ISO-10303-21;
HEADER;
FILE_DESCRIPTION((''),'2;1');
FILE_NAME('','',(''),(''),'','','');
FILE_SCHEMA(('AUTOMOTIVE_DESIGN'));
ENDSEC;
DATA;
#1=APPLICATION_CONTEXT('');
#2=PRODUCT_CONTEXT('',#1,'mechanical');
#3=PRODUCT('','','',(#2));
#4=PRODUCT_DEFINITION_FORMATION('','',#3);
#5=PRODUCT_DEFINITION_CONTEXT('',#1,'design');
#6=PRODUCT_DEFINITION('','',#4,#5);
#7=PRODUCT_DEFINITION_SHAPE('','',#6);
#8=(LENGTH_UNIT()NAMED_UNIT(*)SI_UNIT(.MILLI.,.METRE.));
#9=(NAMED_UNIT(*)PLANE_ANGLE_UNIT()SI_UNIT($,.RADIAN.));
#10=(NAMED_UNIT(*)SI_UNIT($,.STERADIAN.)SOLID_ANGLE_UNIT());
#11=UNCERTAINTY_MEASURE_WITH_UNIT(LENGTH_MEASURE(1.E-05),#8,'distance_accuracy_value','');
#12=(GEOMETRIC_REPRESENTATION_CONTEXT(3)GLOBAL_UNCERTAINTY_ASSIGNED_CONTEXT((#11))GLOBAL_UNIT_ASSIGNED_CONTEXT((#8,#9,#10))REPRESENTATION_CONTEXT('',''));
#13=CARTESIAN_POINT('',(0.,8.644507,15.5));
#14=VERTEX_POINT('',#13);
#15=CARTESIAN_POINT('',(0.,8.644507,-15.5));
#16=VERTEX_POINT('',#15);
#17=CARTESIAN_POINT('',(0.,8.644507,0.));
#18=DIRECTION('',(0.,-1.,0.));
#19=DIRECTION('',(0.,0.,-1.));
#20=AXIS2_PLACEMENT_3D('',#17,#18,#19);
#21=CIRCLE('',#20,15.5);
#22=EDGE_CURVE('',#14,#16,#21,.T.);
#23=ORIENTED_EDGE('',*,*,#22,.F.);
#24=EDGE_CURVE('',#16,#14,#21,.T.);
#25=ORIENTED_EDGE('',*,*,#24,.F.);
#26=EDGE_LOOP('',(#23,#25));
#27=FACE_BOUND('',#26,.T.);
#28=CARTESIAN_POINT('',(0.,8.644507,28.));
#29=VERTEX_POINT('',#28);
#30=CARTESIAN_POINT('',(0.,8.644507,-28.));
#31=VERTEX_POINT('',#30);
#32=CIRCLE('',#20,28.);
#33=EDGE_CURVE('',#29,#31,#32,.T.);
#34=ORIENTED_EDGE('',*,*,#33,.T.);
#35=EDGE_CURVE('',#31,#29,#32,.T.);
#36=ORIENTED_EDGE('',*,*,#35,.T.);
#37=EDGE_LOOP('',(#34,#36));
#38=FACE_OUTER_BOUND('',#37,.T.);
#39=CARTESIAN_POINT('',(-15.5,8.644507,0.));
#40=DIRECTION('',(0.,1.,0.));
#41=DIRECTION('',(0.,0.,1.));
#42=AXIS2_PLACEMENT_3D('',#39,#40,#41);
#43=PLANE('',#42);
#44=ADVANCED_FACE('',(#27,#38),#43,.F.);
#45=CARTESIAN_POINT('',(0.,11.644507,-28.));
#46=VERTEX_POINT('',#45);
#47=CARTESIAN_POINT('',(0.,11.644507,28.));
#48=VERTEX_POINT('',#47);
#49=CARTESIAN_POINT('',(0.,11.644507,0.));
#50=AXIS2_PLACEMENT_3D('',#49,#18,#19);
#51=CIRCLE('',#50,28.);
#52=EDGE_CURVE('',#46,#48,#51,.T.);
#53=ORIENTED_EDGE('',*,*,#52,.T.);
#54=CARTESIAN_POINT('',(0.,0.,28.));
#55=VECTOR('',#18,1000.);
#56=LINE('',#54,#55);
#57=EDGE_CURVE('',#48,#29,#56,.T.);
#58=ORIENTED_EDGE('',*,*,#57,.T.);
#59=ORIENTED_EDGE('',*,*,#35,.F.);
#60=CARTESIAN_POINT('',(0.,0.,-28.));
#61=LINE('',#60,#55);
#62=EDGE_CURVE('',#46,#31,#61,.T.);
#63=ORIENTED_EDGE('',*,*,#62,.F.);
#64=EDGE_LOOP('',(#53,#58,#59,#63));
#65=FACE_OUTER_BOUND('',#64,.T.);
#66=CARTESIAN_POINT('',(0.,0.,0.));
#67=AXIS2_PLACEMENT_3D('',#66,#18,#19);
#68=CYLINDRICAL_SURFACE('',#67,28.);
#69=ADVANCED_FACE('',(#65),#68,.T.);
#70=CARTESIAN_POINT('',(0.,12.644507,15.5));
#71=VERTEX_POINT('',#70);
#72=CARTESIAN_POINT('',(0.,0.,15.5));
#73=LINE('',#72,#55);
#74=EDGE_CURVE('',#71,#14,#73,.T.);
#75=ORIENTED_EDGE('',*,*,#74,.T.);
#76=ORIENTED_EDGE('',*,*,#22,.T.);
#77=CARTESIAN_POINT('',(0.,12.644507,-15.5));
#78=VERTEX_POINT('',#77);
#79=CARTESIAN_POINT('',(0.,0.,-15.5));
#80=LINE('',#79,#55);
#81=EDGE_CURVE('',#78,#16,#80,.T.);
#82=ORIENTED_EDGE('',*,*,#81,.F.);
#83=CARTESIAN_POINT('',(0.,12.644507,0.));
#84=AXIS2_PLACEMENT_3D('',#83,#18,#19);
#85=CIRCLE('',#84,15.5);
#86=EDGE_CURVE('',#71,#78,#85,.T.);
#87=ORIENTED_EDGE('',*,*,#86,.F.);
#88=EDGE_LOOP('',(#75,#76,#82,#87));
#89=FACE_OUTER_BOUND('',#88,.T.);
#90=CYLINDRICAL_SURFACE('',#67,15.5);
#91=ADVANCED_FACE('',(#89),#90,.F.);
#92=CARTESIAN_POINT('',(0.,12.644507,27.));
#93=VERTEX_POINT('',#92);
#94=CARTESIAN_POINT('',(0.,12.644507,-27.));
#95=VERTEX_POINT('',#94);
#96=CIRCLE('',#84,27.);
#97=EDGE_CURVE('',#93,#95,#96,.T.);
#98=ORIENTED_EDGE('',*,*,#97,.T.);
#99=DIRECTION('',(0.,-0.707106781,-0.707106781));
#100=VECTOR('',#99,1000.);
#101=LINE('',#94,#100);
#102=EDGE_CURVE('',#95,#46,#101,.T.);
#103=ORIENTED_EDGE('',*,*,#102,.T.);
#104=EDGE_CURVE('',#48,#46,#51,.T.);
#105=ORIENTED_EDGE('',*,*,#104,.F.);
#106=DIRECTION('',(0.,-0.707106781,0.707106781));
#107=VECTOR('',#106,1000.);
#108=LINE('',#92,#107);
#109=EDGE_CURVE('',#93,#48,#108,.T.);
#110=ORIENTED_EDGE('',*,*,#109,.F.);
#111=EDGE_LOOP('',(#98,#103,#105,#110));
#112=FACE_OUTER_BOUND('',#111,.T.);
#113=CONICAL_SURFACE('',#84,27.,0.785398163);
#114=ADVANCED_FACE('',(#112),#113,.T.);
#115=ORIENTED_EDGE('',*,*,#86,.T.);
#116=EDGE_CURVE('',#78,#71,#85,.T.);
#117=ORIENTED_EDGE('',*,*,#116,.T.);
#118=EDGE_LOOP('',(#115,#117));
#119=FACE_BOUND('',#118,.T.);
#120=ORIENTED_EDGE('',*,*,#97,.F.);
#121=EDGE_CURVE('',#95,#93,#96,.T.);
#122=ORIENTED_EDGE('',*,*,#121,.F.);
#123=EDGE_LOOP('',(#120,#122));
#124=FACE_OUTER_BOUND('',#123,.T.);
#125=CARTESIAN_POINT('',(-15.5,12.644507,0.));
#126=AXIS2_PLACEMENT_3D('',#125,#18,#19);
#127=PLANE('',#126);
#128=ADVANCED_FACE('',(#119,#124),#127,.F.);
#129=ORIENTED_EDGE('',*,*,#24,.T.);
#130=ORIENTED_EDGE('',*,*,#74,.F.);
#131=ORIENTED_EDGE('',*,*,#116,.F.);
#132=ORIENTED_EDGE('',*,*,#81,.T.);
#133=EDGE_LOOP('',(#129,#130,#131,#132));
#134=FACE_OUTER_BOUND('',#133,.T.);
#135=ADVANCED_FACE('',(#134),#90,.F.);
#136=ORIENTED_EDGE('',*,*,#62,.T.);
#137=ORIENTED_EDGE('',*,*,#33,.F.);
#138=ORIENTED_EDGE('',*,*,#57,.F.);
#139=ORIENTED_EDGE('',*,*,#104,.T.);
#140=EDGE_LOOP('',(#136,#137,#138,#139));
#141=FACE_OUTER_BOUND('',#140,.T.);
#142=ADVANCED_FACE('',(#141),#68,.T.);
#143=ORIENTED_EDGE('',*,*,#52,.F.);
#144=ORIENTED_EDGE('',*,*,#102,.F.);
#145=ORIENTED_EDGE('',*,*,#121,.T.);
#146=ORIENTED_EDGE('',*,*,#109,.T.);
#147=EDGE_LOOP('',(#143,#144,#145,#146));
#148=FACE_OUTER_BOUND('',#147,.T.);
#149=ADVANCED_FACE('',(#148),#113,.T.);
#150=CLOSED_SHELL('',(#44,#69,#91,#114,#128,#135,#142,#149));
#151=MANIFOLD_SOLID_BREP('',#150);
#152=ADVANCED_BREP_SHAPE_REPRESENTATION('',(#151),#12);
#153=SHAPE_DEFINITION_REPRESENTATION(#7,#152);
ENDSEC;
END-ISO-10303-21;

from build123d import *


with BuildPart() as part:
    # Sketch1 → Base-Revolve (revolve)
    with BuildSketch(Plane.XY, mode=Mode.PRIVATE) as base_revolve_sk:
        Polygon((-27, 12.644507042), (-28, 11.644507042), (-28, 8.644507042), (-15.5, 8.644507042), (-15.5, 12.644507042), align=None)
    revolve(base_revolve_sk.sketch.rotate(Axis((0, 0, 0), (0, 1, 0)), 270), axis=Axis((0, 0, 0), (0, 1, 0)))


solid = part.part
